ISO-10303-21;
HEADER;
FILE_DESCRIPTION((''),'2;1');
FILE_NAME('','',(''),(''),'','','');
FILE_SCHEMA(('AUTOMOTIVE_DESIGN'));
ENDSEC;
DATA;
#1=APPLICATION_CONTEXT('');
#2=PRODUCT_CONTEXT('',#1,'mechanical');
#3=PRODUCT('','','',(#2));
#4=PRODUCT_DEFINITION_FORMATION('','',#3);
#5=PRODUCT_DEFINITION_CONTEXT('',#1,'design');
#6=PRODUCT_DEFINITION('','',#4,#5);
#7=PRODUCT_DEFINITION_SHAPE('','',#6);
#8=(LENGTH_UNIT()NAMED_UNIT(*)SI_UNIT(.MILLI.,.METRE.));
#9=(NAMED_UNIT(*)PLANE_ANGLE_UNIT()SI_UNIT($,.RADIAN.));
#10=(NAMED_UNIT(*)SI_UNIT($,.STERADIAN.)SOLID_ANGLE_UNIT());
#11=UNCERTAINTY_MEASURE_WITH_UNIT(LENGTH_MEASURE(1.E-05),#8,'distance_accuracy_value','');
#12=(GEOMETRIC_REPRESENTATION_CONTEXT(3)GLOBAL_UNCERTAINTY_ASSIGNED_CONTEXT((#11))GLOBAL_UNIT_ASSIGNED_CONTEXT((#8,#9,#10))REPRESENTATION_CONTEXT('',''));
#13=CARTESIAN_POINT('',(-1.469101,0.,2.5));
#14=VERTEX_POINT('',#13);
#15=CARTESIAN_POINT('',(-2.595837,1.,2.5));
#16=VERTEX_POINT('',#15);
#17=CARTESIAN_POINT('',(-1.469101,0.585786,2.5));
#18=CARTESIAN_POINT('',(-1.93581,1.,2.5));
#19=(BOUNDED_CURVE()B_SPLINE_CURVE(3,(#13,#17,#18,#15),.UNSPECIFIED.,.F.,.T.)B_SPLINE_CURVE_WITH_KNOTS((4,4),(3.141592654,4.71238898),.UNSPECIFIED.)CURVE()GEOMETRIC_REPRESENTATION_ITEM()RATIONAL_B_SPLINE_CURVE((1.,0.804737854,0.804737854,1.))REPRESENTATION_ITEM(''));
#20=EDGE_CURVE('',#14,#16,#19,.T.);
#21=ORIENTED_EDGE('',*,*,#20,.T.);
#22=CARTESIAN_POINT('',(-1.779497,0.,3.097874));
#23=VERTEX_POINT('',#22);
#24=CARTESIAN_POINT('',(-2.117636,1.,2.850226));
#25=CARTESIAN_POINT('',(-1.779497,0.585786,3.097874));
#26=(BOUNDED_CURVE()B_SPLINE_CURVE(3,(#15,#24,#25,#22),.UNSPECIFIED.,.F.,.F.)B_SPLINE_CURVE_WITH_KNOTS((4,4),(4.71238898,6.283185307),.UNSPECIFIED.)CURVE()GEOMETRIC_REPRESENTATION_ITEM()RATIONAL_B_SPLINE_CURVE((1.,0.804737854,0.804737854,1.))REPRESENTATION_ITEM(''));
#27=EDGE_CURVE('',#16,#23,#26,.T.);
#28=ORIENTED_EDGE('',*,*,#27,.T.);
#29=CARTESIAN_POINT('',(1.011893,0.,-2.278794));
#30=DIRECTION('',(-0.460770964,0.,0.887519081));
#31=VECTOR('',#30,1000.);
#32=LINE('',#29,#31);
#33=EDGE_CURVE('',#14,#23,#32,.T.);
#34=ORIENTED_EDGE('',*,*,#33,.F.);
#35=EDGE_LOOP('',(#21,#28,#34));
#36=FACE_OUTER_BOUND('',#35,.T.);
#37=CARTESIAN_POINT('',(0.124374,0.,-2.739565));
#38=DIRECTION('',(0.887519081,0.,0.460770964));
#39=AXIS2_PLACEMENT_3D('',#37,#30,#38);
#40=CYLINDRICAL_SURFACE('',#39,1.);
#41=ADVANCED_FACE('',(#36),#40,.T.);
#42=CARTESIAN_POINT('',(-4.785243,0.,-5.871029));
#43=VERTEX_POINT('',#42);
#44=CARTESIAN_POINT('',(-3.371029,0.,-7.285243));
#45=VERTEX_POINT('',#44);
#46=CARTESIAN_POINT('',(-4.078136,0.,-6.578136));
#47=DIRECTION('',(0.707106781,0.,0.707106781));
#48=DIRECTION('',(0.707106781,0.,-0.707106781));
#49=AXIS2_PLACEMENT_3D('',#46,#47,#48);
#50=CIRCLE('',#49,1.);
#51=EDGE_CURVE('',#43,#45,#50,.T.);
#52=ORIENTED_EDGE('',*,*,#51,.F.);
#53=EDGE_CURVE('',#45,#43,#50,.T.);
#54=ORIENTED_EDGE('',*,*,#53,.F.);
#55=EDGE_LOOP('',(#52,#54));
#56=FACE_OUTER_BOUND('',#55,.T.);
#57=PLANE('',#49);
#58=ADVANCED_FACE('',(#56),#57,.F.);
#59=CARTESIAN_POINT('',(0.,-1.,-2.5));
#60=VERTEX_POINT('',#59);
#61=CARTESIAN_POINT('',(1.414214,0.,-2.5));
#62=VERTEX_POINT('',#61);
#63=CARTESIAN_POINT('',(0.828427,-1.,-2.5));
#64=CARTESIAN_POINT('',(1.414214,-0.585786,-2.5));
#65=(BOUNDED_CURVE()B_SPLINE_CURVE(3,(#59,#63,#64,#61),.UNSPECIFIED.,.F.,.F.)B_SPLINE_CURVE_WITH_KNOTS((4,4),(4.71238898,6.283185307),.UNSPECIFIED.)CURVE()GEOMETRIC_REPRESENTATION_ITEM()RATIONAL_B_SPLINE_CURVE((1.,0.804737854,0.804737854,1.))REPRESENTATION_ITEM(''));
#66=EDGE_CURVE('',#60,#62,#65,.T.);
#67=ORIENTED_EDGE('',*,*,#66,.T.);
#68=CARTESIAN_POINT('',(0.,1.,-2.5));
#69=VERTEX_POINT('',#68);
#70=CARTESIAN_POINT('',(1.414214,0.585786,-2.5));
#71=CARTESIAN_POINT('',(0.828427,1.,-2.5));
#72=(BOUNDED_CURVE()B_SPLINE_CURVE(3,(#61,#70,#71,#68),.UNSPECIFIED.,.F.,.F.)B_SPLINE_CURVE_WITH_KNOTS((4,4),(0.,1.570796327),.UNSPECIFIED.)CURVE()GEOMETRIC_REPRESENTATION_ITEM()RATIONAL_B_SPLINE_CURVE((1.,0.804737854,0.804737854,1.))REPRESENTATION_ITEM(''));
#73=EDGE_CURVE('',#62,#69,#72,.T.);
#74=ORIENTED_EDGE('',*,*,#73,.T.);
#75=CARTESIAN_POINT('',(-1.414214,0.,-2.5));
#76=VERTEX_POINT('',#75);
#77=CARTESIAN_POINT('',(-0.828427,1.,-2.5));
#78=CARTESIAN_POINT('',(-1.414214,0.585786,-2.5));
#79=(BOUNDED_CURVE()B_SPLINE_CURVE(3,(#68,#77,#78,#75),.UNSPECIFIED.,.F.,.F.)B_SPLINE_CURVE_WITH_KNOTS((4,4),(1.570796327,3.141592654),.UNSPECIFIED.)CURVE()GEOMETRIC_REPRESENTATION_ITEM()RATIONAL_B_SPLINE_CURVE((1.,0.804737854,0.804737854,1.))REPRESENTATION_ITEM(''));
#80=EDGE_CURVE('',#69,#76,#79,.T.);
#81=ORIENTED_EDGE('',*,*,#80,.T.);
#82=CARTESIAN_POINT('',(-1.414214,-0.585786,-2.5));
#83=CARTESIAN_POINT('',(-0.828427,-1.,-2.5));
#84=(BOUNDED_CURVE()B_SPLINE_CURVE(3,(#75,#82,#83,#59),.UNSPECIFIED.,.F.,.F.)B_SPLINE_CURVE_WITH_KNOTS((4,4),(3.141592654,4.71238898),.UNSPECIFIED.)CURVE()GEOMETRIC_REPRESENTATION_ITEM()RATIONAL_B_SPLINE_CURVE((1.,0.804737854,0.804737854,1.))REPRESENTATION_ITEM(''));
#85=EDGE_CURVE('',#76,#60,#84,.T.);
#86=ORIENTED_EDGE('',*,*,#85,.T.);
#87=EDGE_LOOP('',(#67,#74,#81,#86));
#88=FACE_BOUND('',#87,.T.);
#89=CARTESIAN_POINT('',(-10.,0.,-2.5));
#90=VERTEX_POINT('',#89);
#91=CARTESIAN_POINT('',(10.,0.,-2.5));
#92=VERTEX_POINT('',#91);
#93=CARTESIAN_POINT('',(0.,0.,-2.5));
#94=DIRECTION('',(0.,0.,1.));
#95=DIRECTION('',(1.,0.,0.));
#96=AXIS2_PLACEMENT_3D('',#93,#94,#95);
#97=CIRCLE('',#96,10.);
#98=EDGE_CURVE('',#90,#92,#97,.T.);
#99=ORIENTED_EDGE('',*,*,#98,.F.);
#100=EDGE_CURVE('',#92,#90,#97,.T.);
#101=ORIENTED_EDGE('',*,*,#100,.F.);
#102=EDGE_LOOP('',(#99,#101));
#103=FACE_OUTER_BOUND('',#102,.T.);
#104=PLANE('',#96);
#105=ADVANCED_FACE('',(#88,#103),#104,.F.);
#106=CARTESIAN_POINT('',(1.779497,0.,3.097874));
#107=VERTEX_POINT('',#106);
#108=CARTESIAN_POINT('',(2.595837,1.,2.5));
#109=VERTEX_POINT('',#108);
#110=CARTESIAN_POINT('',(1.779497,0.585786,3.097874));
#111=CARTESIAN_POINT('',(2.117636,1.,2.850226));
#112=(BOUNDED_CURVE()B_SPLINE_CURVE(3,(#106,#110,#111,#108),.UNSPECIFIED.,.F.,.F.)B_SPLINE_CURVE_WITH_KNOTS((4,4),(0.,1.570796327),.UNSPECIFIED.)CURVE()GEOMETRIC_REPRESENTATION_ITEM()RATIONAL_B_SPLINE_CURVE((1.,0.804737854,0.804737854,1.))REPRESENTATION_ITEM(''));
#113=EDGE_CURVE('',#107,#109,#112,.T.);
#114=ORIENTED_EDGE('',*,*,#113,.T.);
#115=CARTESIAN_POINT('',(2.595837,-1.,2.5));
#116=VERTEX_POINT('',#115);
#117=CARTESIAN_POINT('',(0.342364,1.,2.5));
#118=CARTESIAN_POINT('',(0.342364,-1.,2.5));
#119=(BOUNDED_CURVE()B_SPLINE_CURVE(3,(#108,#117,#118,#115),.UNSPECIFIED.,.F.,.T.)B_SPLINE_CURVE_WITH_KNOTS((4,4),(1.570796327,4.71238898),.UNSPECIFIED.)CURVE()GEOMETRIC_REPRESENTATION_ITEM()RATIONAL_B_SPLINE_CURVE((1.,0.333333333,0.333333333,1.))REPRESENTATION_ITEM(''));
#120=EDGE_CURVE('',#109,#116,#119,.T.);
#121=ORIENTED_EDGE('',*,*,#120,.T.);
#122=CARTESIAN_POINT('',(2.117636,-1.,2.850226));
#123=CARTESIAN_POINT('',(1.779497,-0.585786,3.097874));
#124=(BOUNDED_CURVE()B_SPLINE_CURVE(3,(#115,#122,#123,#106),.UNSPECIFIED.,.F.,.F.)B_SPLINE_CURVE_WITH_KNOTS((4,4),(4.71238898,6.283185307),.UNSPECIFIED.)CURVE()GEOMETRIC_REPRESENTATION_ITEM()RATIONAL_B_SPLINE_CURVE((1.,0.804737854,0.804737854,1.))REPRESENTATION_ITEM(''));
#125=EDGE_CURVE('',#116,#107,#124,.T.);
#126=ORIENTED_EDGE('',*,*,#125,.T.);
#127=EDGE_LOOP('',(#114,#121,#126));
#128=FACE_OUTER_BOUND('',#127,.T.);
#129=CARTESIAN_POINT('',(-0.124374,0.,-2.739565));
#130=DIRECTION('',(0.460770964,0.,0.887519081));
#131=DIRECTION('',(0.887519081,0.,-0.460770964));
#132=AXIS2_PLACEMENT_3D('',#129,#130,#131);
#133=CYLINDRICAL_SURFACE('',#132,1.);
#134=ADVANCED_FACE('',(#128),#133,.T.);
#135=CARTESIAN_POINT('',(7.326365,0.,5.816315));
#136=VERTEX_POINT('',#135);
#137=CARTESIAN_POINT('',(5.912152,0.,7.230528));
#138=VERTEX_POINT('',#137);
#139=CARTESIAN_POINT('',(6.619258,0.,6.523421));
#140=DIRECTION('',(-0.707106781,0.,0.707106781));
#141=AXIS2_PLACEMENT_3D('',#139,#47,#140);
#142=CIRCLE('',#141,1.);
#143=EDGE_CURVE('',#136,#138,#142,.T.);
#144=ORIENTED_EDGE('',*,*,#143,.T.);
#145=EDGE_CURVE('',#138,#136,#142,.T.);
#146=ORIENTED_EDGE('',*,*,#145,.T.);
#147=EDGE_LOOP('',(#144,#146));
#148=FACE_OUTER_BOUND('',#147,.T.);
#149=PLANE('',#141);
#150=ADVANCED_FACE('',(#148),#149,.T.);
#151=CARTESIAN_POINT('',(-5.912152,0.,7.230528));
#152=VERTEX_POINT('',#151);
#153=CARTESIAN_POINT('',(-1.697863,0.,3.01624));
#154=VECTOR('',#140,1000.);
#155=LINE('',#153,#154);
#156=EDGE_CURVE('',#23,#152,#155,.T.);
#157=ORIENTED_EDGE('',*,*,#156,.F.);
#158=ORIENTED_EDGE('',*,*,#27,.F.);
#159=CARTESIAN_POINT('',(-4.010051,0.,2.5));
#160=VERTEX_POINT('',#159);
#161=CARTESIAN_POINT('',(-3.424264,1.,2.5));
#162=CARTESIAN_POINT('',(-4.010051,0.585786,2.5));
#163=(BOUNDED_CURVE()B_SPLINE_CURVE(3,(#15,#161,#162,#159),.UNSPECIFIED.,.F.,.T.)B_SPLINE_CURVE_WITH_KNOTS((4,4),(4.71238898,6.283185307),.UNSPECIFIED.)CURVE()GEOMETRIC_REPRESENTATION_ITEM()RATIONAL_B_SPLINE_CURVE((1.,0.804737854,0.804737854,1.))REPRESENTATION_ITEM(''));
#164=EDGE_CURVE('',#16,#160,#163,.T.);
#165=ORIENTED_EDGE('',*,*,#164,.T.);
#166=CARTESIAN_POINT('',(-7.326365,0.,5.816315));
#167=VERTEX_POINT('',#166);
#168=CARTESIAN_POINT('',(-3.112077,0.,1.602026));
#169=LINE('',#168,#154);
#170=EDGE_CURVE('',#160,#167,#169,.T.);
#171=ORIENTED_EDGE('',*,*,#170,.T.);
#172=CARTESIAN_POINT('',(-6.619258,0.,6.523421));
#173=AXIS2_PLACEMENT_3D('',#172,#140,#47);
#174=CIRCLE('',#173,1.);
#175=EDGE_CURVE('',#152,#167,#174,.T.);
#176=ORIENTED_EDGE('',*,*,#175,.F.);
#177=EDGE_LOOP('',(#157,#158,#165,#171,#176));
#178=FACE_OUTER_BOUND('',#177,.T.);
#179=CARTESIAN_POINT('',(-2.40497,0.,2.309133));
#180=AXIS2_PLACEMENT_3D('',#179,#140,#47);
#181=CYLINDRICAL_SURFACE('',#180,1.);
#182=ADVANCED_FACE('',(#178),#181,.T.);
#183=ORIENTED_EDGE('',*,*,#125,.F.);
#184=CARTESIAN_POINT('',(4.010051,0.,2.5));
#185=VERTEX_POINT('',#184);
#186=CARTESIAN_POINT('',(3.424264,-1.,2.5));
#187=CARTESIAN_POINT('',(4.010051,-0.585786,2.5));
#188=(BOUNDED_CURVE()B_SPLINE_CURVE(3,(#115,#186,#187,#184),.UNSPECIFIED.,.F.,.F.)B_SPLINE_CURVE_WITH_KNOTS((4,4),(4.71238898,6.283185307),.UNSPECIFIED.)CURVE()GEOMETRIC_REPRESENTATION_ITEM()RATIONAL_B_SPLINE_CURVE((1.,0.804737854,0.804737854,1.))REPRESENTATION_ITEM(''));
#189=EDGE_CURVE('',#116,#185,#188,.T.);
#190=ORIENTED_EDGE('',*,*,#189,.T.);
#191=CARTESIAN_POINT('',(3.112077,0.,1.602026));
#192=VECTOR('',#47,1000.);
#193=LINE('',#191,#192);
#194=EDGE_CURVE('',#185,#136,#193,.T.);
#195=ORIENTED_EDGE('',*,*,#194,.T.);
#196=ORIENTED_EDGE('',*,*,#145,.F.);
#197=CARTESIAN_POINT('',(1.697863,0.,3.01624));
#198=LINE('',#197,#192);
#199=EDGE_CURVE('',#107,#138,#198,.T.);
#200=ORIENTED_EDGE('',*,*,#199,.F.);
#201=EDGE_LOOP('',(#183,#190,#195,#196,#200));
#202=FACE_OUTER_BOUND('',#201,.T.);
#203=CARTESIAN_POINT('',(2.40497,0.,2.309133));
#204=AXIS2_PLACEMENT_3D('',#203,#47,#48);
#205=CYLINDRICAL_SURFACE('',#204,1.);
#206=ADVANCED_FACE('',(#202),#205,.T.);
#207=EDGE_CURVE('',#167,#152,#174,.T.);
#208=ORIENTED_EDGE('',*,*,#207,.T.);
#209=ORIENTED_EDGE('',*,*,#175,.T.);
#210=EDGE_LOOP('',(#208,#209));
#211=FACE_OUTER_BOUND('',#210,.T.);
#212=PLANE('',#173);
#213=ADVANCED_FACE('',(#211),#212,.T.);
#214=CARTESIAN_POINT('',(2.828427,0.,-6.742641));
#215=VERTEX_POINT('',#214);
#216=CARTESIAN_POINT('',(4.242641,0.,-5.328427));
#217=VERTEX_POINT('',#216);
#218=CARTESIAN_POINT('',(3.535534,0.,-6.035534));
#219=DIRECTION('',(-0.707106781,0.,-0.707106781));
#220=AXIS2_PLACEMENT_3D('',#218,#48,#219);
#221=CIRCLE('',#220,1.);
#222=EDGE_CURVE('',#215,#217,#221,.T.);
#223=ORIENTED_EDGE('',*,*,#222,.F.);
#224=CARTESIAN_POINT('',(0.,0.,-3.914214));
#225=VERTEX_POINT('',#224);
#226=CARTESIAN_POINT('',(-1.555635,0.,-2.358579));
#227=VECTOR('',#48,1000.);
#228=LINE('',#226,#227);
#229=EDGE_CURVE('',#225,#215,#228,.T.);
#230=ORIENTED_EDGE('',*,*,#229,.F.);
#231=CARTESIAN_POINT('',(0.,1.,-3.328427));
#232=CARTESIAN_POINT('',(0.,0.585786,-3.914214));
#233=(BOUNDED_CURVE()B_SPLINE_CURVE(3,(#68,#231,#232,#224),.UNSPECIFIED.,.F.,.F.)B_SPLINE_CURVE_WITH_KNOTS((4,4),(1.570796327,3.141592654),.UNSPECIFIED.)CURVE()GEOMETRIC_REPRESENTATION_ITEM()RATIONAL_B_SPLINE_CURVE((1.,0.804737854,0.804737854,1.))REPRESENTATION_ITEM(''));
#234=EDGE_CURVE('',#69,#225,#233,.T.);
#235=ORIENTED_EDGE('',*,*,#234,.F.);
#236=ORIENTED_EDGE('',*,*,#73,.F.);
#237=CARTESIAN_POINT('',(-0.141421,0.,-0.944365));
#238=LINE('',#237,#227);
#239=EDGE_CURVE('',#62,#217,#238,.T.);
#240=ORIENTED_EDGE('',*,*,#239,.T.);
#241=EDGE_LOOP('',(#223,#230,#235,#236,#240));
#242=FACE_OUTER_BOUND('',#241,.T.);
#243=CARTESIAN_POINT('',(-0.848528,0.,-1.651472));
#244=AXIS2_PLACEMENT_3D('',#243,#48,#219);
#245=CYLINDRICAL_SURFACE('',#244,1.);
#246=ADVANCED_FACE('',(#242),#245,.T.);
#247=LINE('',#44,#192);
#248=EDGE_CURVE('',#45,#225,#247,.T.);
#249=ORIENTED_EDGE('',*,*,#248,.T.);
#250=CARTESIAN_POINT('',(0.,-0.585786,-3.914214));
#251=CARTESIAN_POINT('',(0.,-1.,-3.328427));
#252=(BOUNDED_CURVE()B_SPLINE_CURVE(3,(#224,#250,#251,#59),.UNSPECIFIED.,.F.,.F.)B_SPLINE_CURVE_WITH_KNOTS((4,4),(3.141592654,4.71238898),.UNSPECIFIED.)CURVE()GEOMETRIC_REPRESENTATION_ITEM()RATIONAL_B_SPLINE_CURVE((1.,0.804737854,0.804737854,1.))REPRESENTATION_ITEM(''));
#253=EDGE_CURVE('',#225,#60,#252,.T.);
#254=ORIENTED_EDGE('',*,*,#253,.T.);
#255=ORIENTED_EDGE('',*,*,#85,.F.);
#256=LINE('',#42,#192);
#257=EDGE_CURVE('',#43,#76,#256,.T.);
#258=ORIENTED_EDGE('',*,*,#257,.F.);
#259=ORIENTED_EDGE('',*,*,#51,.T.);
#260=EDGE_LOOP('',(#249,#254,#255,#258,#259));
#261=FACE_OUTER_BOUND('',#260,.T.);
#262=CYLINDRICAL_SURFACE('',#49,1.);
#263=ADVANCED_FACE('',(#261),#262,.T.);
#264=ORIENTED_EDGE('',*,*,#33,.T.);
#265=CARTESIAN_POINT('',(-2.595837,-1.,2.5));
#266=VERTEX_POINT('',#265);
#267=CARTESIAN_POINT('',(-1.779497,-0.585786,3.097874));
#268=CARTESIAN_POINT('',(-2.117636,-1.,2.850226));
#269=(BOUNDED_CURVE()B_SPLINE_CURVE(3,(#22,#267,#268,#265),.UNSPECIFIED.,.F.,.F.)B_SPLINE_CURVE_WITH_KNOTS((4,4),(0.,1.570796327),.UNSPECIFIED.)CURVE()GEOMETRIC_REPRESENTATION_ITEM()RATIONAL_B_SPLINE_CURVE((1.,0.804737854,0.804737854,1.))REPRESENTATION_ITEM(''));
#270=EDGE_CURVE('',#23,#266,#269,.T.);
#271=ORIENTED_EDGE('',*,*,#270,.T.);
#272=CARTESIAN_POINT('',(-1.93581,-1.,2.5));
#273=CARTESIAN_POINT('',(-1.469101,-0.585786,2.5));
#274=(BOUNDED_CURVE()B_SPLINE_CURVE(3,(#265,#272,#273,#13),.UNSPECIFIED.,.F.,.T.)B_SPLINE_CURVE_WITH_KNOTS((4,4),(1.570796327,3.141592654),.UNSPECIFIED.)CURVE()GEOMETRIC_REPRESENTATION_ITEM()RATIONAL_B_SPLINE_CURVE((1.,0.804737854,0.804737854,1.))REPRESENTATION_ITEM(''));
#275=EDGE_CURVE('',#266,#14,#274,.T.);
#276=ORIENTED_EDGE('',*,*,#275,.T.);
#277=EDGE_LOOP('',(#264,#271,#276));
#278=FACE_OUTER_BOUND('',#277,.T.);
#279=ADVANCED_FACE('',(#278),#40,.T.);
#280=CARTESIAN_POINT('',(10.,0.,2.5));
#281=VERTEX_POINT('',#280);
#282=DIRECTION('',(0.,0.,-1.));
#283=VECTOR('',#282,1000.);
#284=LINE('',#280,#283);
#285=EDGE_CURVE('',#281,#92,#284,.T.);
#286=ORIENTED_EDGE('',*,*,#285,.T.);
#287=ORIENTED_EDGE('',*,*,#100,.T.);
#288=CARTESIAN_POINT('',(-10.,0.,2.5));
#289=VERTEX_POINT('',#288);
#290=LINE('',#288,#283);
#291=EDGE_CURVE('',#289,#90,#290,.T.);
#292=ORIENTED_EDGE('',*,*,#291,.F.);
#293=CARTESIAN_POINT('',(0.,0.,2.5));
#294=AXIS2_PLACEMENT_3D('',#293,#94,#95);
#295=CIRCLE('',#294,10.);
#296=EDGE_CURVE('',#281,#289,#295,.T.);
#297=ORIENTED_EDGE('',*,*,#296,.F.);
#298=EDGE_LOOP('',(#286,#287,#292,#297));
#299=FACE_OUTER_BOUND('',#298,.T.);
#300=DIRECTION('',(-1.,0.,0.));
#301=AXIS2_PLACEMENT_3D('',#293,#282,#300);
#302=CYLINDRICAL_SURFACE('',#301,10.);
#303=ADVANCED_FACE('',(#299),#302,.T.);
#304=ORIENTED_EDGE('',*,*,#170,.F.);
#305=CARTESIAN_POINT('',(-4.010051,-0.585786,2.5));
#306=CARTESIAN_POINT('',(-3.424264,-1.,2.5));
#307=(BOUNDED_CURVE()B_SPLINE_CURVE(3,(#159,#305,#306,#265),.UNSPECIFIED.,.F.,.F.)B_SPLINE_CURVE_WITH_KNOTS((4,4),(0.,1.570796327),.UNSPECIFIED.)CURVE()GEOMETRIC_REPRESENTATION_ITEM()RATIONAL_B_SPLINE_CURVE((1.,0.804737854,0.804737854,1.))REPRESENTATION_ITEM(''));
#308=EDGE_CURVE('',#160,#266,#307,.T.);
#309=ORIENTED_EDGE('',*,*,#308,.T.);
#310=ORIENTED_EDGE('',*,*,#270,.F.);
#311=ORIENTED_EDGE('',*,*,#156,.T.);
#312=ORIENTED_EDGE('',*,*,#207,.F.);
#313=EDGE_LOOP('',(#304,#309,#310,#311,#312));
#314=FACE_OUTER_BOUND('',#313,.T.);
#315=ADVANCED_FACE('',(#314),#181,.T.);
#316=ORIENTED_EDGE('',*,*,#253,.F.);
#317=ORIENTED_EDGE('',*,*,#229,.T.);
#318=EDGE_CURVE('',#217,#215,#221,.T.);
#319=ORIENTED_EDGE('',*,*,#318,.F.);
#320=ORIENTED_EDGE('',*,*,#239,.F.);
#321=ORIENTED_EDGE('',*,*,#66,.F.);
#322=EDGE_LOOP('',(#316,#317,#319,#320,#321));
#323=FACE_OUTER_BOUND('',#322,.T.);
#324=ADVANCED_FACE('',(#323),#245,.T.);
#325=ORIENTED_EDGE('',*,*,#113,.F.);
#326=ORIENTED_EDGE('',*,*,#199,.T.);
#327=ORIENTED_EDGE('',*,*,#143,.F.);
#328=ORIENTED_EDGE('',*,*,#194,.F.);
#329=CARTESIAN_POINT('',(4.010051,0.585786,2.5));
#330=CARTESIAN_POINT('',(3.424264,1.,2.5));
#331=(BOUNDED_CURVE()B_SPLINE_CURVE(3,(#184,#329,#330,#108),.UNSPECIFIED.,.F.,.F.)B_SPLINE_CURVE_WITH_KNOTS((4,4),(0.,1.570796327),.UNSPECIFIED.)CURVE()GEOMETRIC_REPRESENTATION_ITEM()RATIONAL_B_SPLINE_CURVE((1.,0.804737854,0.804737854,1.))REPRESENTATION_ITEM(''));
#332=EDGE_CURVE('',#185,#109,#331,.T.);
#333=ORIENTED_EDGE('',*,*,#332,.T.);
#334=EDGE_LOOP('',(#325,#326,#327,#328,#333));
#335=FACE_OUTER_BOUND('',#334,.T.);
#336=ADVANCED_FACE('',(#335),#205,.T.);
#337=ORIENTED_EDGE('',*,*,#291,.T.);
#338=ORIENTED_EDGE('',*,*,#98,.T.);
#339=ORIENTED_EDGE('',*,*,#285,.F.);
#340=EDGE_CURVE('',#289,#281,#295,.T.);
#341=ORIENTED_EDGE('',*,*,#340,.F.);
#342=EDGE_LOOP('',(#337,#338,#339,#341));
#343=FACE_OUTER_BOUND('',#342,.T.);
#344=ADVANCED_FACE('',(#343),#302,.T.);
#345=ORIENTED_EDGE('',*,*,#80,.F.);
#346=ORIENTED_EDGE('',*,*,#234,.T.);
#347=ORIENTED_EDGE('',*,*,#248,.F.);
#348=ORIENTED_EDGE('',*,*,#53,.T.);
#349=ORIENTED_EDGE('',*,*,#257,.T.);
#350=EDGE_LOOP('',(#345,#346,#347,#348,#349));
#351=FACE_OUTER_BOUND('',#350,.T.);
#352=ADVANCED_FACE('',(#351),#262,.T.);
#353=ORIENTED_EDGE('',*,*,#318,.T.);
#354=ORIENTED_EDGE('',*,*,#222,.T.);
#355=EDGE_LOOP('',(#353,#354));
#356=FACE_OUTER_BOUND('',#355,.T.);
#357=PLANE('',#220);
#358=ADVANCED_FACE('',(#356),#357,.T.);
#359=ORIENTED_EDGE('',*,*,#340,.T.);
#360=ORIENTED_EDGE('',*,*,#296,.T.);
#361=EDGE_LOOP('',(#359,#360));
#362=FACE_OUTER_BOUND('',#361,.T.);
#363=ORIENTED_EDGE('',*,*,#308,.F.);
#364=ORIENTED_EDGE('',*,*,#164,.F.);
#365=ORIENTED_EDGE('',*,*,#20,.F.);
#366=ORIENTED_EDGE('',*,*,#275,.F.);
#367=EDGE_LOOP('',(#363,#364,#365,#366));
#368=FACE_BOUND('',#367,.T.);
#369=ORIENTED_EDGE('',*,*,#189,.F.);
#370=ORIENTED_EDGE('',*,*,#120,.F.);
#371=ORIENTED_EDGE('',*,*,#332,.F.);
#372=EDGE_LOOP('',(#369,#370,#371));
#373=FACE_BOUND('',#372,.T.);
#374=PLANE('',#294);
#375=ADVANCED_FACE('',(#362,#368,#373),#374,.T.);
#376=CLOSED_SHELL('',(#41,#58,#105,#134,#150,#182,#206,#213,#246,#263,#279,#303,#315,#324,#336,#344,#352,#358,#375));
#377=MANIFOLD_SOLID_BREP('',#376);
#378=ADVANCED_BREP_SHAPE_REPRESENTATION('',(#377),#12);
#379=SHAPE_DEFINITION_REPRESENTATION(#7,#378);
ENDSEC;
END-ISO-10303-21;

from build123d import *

# Parameters (mm, degrees)
SKETCH1_R           = 10
BOSS_EXTRUDE1_DEPTH = 2.5
SKETCH5_R           = 1
SKETCH7_R           = 1


with BuildPart() as part:
    # Sketch1 → Boss-Extrude1 (new, symmetric)
    with BuildSketch(Plane.XY):
        Circle(SKETCH1_R)
    extrude(amount=BOSS_EXTRUDE1_DEPTH, both=True)

    # Sweep1: sweep along a path in Sketch3
    with BuildLine(Plane(origin=(0, 0, 0), x_dir=(1, 0, 0), z_dir=(0, 1, 0))) as sweep1_path:
        Line((-4.078135837, 6.578135837), (0, 2.5))
        Line((0, 2.5), (3.535533906, 6.035533906))
    # Sketch5 → Sweep1 (sweep)
    with BuildSketch(Plane(origin=(3.535533906, 0, -6.035533906), x_dir=(-0.7071067811865517, 0, -0.7071067811865434), z_dir=(0.7071067811865434, 0, -0.7071067811865517))):
        Circle(SKETCH5_R)
    sweep(path=sweep1_path.line, transition=Transition.RIGHT)

    # Sweep2: sweep along a path in Sketch8
    with BuildLine(Plane(origin=(0, 0, 0), x_dir=(1, 0, 0), z_dir=(0, 1, 0))) as sweep2_path:
        Line((3.535533906, 6.035533906), (0, 2.5))
        Line((0, 2.5), (-2.595836944, -2.5))
        Line((-2.595836944, -2.5), (-6.619258355, -6.523421411))
    # Sketch7 → Sweep2 (sweep)
    with BuildSketch(Plane(origin=(-6.619258355, 0, 6.523421411), x_dir=(0.7071067811865527, 0, 0.7071067811865425), z_dir=(-0.7071067811865425, 0, 0.7071067811865527))):
        Circle(SKETCH7_R)
    sweep2 = sweep(path=sweep2_path.line, transition=Transition.RIGHT)

    # Mirror1: Sweep2 across plane
    add(sweep2.mirror(Plane(origin=(0, 0, 0), x_dir=(0, 0, 1), z_dir=(1, 0, 0))))


solid = part.part
